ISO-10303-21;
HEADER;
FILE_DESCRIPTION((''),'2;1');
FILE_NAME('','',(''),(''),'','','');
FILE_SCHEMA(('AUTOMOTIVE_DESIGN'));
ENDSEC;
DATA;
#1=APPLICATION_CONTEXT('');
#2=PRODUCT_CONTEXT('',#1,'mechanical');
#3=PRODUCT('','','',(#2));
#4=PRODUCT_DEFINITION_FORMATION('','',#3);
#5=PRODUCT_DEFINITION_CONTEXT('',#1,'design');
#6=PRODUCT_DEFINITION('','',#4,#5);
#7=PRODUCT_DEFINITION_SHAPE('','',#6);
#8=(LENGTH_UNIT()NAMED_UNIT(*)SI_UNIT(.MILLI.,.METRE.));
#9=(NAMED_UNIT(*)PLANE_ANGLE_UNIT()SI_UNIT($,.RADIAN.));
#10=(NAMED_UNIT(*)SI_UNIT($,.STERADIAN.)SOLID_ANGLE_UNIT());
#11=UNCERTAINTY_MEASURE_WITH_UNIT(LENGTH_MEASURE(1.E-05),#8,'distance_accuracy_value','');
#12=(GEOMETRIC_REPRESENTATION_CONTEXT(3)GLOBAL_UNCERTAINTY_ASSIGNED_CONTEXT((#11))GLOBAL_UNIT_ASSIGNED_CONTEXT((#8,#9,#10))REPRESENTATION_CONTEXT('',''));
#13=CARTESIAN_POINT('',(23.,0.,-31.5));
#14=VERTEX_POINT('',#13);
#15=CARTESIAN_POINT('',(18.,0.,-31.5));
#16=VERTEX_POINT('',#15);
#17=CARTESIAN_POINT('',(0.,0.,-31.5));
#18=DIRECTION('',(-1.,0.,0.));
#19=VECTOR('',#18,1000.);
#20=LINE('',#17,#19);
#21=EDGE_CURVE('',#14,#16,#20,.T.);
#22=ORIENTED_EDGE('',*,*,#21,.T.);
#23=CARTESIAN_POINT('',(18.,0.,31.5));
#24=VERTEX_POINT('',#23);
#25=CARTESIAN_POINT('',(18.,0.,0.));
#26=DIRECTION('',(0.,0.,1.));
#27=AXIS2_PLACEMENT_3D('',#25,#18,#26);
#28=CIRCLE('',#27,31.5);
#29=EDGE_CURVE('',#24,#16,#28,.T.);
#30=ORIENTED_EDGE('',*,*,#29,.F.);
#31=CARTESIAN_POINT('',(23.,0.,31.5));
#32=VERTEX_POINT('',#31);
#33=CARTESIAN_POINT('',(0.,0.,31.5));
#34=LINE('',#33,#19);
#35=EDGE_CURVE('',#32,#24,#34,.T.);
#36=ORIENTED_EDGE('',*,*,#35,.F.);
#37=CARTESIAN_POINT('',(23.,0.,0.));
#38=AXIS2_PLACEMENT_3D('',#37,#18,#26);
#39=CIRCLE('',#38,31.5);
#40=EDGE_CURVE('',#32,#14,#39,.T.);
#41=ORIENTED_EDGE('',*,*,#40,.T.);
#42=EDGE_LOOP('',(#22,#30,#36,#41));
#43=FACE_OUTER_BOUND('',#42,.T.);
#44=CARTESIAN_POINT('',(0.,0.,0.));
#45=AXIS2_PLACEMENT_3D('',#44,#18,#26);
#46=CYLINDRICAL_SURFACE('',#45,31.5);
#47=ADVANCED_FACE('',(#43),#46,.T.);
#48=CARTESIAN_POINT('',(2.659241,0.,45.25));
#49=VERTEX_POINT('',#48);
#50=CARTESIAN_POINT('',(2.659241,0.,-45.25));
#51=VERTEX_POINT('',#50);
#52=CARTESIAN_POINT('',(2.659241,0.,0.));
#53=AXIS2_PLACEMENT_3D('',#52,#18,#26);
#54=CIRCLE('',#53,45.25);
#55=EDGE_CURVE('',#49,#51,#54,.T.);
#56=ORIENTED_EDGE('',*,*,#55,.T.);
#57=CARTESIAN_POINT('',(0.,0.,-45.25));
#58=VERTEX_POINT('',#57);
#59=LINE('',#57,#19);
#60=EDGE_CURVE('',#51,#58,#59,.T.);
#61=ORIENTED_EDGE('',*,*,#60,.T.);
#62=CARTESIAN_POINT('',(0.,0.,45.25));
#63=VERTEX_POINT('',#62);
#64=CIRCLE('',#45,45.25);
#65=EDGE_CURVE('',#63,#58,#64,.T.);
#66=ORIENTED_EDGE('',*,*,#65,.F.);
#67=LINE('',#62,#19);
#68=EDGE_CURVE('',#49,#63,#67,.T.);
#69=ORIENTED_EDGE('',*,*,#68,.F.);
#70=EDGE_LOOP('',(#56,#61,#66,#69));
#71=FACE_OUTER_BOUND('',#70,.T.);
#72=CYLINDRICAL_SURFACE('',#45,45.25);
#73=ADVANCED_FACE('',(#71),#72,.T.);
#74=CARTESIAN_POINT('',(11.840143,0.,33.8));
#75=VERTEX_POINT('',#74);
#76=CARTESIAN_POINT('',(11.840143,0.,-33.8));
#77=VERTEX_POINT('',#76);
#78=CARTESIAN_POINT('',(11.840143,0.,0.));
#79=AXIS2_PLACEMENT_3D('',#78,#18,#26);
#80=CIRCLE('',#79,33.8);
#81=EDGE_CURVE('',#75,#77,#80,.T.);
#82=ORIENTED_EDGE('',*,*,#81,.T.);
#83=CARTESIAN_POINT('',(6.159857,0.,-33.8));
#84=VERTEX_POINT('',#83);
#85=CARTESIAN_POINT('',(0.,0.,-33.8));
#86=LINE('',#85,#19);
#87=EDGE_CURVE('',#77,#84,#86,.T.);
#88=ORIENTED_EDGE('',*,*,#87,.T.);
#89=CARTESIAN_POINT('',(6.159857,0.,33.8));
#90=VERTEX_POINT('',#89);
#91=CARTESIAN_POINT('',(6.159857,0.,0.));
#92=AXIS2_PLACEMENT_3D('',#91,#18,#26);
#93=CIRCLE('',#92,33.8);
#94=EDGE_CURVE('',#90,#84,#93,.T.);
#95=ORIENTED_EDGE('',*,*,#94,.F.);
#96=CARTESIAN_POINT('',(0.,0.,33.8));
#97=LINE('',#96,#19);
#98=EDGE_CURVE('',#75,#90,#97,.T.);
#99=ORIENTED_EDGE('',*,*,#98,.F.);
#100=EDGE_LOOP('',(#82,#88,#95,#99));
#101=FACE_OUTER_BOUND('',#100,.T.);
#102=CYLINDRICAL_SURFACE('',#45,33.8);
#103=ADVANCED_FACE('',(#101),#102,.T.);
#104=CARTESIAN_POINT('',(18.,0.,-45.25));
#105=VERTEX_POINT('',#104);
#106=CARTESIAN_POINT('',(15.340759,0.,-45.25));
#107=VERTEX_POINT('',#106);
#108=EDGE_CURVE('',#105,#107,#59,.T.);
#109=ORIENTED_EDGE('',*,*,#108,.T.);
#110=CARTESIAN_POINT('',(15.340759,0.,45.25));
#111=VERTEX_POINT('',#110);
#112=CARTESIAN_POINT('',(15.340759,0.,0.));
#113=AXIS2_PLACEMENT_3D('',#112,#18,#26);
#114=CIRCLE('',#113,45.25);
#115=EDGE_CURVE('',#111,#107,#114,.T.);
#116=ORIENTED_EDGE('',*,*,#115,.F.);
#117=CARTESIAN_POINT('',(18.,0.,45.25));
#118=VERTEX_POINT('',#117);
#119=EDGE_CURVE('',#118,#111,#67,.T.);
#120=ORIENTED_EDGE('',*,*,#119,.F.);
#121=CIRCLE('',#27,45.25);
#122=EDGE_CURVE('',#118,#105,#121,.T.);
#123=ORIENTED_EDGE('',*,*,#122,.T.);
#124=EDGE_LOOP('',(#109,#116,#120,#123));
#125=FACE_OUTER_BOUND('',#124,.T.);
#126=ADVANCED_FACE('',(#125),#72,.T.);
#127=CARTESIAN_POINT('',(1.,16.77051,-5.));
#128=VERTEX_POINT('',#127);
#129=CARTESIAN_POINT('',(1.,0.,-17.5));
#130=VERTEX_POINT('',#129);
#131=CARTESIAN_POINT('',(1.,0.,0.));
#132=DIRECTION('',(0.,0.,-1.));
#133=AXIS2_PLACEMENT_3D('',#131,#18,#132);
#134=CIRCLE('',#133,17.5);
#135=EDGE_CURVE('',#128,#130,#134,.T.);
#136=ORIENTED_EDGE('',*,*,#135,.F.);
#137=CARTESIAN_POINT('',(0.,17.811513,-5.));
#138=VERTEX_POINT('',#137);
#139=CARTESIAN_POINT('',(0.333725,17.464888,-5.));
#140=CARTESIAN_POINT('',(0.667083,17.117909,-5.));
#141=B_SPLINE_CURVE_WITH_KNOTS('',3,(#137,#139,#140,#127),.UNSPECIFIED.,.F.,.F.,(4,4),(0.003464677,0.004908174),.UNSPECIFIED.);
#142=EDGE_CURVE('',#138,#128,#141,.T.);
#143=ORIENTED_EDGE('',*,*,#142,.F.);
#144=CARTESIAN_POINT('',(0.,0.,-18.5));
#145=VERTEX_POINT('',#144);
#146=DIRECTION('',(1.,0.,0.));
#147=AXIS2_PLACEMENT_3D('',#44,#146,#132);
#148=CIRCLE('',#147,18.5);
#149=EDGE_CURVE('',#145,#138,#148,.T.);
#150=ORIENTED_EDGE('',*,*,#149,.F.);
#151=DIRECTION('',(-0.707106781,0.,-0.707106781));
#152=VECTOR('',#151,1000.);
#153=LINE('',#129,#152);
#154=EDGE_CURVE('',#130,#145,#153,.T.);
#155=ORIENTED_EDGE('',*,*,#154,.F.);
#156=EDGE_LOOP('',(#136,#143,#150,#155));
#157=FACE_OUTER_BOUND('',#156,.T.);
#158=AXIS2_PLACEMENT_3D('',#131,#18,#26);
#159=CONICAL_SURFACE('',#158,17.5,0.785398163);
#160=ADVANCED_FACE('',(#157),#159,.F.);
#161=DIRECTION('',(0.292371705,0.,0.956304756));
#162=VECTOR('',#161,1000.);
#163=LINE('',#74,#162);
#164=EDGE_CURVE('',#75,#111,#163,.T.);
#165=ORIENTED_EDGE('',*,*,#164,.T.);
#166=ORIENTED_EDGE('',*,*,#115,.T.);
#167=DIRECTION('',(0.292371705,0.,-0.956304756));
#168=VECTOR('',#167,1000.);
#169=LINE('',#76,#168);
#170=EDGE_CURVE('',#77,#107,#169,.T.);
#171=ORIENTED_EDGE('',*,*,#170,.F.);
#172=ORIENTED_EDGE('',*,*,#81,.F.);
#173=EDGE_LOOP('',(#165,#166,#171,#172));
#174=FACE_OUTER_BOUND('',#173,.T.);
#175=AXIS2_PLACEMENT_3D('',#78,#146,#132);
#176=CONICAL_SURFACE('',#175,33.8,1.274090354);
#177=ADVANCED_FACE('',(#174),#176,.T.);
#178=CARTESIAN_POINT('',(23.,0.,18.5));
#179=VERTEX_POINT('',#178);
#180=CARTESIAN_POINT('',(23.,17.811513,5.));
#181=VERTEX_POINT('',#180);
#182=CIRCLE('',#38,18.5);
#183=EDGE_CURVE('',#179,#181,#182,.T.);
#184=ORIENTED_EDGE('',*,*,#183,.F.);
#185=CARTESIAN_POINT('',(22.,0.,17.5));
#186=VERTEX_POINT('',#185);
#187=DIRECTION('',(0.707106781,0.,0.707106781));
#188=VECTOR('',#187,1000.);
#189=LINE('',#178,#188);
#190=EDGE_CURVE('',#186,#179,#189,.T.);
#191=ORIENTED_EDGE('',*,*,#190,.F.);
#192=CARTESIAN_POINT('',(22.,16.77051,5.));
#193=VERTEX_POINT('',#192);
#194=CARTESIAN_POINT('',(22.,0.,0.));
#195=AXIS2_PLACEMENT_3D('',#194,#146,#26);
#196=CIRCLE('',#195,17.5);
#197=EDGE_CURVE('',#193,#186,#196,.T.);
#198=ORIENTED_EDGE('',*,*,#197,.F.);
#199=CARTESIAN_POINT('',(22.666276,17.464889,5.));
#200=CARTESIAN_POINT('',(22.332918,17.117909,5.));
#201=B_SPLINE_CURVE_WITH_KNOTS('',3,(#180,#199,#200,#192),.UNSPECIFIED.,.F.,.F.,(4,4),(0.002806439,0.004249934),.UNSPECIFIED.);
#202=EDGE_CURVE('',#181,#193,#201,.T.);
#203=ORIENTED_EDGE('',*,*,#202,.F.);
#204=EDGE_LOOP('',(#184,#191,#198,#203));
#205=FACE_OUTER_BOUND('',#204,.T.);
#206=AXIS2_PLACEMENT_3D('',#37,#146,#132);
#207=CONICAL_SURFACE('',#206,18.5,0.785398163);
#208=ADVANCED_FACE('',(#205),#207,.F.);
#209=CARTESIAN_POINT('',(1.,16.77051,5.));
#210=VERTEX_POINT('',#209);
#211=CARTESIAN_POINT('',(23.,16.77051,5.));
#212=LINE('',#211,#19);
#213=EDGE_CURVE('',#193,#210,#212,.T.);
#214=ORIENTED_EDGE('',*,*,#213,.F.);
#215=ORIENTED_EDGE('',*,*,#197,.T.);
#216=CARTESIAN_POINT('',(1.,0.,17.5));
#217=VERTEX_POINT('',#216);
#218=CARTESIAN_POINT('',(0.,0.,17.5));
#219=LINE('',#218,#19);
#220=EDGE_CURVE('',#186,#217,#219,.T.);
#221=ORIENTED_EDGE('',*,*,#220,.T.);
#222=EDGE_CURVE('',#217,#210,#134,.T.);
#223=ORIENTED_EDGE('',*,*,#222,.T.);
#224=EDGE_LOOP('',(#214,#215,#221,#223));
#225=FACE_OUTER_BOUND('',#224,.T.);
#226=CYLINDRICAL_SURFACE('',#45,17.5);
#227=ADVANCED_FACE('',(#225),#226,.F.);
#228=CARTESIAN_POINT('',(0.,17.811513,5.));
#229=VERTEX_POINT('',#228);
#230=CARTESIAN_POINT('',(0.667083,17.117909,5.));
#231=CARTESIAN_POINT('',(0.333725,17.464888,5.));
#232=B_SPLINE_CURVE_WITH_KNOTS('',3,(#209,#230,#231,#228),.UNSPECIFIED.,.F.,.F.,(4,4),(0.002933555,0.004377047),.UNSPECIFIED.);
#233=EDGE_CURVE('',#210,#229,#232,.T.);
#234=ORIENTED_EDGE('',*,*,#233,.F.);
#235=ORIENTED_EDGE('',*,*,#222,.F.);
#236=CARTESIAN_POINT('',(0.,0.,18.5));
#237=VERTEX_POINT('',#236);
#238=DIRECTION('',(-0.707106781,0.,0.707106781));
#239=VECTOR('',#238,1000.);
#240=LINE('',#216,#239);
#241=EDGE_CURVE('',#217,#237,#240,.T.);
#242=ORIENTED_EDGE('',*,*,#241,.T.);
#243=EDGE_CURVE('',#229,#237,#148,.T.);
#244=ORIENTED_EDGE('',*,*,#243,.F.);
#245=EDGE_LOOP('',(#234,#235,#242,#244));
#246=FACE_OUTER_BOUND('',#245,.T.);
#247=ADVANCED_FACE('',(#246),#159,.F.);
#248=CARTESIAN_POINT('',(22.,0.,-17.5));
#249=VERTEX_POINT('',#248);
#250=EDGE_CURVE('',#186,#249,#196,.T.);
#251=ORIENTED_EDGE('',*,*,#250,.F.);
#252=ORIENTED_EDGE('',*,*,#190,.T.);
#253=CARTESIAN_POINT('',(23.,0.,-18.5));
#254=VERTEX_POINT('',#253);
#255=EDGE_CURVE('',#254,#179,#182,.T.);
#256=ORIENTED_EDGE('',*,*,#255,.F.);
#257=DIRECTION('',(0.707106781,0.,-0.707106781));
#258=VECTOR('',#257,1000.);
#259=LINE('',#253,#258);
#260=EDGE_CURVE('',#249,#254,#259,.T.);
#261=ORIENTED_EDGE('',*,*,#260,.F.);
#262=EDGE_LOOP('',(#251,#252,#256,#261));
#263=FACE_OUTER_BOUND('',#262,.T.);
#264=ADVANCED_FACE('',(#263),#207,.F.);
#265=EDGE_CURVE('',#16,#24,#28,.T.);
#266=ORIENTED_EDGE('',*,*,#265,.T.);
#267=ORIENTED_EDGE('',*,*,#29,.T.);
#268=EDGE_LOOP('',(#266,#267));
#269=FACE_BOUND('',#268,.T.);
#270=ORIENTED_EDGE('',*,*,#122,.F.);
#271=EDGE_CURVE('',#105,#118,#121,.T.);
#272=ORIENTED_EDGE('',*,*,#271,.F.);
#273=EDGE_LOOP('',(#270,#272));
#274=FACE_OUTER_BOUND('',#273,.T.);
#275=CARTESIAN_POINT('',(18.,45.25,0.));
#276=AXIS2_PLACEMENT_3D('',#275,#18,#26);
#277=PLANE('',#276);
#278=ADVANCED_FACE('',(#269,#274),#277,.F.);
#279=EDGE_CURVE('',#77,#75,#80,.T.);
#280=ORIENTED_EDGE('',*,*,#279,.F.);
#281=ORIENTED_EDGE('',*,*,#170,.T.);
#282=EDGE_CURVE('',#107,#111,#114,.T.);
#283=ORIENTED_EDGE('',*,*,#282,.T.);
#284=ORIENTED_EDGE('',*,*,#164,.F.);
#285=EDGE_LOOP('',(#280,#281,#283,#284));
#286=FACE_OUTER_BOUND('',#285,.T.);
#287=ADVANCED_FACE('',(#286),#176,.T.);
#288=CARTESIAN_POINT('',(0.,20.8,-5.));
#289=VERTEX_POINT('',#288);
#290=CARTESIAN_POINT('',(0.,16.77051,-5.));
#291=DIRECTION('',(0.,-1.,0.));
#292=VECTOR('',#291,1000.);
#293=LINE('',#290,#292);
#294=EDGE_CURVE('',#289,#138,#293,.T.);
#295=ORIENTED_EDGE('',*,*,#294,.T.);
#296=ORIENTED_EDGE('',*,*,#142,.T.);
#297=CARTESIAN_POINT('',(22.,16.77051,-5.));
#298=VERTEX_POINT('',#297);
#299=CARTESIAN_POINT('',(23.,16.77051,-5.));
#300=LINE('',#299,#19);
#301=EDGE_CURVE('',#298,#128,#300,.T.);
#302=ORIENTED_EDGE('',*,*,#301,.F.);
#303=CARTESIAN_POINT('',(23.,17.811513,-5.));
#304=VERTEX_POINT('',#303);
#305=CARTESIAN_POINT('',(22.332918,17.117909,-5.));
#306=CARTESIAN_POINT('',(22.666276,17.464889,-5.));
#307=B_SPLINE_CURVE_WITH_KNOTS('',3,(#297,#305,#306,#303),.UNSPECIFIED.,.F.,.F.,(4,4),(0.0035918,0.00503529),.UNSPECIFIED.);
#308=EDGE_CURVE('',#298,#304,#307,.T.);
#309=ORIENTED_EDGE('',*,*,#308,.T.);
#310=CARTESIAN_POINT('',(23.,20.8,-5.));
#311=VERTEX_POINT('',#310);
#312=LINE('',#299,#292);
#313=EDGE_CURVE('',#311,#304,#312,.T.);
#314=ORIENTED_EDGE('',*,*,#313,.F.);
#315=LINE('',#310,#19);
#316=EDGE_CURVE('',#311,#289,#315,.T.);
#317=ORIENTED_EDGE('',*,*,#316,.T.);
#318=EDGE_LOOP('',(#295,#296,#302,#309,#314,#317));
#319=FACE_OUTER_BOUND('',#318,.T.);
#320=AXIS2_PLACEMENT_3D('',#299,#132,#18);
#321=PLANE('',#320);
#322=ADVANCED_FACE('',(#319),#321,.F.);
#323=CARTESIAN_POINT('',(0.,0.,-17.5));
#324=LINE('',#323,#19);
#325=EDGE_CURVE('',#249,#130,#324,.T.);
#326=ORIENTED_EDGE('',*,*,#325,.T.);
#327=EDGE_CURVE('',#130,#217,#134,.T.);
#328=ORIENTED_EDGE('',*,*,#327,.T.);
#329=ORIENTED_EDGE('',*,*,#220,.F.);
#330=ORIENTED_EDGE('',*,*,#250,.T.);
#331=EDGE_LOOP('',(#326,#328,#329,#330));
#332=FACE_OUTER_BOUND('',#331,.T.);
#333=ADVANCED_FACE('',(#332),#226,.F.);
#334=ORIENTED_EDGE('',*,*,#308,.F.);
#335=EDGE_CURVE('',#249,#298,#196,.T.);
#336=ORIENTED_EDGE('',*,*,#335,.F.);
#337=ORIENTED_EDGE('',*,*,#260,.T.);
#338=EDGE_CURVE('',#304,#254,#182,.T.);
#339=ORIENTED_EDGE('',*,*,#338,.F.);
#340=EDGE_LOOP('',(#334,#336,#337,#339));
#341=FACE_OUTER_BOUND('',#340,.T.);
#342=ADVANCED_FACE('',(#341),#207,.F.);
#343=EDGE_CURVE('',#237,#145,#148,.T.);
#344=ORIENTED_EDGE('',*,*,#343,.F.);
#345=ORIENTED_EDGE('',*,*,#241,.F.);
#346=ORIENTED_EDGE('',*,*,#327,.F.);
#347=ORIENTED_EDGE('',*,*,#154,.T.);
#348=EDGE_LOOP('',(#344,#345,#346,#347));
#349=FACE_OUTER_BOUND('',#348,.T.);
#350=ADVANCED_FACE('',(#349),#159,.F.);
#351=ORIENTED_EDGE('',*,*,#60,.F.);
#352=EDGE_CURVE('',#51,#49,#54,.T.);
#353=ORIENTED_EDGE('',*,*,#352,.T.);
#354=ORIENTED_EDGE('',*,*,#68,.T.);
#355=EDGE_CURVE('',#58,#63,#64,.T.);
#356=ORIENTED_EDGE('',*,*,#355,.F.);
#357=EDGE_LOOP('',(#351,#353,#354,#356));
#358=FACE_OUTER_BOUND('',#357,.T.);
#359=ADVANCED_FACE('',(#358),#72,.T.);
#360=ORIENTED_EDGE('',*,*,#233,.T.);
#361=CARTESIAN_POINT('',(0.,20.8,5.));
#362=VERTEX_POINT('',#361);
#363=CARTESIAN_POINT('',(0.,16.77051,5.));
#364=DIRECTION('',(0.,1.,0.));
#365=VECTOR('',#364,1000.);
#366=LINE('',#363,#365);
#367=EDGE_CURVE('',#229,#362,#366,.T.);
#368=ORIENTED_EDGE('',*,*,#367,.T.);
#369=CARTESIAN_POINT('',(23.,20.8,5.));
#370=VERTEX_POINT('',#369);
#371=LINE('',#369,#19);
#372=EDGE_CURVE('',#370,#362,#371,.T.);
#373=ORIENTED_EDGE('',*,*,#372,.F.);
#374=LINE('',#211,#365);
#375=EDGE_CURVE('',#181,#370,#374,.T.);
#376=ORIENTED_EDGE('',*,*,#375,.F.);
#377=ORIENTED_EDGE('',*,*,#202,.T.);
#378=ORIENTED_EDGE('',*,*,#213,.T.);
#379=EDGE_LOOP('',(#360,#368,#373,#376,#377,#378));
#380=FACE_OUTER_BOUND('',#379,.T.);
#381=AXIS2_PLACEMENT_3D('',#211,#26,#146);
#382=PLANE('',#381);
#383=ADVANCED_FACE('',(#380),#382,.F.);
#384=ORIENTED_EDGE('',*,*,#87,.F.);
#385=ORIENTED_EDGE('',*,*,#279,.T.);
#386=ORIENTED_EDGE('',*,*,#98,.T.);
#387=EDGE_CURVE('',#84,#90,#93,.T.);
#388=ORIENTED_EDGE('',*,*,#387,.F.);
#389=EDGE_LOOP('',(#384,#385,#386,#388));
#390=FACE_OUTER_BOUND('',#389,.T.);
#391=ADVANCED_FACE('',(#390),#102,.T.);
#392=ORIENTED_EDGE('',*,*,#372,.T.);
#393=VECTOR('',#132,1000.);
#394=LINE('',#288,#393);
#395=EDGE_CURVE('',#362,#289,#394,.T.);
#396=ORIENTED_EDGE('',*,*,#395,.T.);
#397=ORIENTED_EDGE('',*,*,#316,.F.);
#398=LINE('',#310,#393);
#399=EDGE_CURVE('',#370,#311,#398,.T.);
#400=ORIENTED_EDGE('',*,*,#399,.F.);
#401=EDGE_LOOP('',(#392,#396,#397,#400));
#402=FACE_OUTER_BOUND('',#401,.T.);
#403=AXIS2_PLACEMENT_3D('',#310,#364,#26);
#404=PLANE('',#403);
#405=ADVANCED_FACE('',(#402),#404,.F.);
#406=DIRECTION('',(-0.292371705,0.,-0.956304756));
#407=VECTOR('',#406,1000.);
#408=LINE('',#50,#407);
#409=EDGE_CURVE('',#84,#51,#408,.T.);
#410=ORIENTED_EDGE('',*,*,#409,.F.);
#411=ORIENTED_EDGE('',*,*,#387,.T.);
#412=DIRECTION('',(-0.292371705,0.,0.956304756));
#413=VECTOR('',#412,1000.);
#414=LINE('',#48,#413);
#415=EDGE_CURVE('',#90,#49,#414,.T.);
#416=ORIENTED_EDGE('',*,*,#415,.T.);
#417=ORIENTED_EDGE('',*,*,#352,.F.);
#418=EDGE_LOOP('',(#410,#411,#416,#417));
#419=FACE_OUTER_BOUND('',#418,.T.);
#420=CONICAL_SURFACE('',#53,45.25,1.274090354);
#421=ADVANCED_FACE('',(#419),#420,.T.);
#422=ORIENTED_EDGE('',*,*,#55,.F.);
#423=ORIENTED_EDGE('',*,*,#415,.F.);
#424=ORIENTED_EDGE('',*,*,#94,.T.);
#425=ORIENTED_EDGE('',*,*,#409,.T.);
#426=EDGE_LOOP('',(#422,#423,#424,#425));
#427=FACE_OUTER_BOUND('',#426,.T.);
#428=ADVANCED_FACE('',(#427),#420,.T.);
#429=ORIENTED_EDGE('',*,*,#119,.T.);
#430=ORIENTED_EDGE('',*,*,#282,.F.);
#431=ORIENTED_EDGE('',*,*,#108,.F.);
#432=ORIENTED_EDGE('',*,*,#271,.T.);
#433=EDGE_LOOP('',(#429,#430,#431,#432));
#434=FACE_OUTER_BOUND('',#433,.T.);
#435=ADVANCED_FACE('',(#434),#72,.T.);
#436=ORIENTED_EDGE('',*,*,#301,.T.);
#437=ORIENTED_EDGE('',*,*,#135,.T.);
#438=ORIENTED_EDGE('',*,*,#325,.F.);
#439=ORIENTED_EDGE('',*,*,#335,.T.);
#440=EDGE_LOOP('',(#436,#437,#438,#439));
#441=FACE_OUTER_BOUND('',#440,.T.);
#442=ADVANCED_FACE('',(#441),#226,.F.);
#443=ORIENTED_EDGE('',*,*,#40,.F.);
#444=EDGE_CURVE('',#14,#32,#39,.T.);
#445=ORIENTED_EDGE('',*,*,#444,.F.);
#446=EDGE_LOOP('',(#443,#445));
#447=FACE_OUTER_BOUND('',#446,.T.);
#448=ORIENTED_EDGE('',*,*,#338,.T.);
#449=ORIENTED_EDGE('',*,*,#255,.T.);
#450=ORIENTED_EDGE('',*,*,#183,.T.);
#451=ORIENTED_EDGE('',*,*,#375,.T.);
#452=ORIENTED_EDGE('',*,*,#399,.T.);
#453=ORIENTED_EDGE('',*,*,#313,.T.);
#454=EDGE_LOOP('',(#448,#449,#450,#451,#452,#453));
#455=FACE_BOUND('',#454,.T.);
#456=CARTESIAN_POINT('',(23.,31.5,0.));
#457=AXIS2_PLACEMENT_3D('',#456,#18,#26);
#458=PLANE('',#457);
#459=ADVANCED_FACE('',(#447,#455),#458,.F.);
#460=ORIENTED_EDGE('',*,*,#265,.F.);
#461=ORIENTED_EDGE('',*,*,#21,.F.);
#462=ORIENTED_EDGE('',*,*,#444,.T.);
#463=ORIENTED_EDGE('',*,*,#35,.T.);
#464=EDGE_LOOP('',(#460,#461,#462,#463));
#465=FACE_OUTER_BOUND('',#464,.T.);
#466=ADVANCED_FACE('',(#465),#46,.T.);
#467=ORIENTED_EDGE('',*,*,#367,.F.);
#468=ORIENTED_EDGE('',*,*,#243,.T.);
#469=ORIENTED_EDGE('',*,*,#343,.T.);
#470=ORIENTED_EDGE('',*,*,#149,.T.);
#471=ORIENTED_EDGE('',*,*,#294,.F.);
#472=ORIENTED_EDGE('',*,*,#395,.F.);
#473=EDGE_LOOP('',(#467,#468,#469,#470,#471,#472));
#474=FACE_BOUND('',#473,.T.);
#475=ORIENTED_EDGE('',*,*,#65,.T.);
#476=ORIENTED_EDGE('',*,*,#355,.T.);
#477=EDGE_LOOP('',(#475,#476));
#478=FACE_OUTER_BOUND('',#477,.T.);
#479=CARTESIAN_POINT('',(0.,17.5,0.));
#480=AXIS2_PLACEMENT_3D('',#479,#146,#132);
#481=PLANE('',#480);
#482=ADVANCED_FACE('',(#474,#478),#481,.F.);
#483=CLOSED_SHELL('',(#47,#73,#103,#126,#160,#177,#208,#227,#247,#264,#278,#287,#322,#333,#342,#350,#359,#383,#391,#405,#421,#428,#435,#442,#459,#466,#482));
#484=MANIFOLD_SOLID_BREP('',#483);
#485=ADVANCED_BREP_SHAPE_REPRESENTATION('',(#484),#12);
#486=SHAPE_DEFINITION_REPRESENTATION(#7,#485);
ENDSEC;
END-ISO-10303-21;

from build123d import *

# Parameters (mm, degrees)
CHAMFER_1_SIZE      = 1
SKETCH_4_W          = 10
SKETCH_4_H          = 4.029490121
CUT_EXTRUDE_1_DEPTH = 69.000919111


with BuildPart() as part:
    # 草图1 → 旋转1 (revolve)
    with BuildSketch(Plane.XY, mode=Mode.PRIVATE) as revolve_1_sk:
        Polygon((0, 17.5), (0, 45.25), (18, 45.25), (18, 31.5), (23, 31.5), (23, 17.5), align=None)
    revolve(revolve_1_sk.sketch.rotate(Axis((0, 0, 0), (1, 0, 0)), 90), axis=Axis((0, 0, 0), (1, 0, 0)))

    # 草图2 → 切除-旋转1 (revolve, cut)
    with BuildSketch(Plane.XY, mode=Mode.PRIVATE) as cut_revolve_1_sk:
        Polygon((11.840143071, 33.8), (15.340759374, 45.25), (2.659240626, 45.25), (6.159856929, 33.8), align=None)
    revolve(cut_revolve_1_sk.sketch.rotate(Axis((0, 0, 0), (1, 0, 0)), 90), axis=Axis((0, 0, 0), (1, 0, 0)), mode=Mode.SUBTRACT)

    # 倒角1
    chamfer_1_edges = [part.edges().sort_by_distance(p)[0] for p in [
        (0, 0, -17.5),
        (23, 0, -17.5),
    ]]
    chamfer(chamfer_1_edges, length=CHAMFER_1_SIZE)

    # 草图4 → 切除-拉伸1 (cut, through all)
    with BuildSketch(Plane.ZY):
        with Locations((0, 18.785254892)):
            Rectangle(SKETCH_4_W, SKETCH_4_H)
    extrude(amount=-CUT_EXTRUDE_1_DEPTH, mode=Mode.SUBTRACT)


solid = part.part
